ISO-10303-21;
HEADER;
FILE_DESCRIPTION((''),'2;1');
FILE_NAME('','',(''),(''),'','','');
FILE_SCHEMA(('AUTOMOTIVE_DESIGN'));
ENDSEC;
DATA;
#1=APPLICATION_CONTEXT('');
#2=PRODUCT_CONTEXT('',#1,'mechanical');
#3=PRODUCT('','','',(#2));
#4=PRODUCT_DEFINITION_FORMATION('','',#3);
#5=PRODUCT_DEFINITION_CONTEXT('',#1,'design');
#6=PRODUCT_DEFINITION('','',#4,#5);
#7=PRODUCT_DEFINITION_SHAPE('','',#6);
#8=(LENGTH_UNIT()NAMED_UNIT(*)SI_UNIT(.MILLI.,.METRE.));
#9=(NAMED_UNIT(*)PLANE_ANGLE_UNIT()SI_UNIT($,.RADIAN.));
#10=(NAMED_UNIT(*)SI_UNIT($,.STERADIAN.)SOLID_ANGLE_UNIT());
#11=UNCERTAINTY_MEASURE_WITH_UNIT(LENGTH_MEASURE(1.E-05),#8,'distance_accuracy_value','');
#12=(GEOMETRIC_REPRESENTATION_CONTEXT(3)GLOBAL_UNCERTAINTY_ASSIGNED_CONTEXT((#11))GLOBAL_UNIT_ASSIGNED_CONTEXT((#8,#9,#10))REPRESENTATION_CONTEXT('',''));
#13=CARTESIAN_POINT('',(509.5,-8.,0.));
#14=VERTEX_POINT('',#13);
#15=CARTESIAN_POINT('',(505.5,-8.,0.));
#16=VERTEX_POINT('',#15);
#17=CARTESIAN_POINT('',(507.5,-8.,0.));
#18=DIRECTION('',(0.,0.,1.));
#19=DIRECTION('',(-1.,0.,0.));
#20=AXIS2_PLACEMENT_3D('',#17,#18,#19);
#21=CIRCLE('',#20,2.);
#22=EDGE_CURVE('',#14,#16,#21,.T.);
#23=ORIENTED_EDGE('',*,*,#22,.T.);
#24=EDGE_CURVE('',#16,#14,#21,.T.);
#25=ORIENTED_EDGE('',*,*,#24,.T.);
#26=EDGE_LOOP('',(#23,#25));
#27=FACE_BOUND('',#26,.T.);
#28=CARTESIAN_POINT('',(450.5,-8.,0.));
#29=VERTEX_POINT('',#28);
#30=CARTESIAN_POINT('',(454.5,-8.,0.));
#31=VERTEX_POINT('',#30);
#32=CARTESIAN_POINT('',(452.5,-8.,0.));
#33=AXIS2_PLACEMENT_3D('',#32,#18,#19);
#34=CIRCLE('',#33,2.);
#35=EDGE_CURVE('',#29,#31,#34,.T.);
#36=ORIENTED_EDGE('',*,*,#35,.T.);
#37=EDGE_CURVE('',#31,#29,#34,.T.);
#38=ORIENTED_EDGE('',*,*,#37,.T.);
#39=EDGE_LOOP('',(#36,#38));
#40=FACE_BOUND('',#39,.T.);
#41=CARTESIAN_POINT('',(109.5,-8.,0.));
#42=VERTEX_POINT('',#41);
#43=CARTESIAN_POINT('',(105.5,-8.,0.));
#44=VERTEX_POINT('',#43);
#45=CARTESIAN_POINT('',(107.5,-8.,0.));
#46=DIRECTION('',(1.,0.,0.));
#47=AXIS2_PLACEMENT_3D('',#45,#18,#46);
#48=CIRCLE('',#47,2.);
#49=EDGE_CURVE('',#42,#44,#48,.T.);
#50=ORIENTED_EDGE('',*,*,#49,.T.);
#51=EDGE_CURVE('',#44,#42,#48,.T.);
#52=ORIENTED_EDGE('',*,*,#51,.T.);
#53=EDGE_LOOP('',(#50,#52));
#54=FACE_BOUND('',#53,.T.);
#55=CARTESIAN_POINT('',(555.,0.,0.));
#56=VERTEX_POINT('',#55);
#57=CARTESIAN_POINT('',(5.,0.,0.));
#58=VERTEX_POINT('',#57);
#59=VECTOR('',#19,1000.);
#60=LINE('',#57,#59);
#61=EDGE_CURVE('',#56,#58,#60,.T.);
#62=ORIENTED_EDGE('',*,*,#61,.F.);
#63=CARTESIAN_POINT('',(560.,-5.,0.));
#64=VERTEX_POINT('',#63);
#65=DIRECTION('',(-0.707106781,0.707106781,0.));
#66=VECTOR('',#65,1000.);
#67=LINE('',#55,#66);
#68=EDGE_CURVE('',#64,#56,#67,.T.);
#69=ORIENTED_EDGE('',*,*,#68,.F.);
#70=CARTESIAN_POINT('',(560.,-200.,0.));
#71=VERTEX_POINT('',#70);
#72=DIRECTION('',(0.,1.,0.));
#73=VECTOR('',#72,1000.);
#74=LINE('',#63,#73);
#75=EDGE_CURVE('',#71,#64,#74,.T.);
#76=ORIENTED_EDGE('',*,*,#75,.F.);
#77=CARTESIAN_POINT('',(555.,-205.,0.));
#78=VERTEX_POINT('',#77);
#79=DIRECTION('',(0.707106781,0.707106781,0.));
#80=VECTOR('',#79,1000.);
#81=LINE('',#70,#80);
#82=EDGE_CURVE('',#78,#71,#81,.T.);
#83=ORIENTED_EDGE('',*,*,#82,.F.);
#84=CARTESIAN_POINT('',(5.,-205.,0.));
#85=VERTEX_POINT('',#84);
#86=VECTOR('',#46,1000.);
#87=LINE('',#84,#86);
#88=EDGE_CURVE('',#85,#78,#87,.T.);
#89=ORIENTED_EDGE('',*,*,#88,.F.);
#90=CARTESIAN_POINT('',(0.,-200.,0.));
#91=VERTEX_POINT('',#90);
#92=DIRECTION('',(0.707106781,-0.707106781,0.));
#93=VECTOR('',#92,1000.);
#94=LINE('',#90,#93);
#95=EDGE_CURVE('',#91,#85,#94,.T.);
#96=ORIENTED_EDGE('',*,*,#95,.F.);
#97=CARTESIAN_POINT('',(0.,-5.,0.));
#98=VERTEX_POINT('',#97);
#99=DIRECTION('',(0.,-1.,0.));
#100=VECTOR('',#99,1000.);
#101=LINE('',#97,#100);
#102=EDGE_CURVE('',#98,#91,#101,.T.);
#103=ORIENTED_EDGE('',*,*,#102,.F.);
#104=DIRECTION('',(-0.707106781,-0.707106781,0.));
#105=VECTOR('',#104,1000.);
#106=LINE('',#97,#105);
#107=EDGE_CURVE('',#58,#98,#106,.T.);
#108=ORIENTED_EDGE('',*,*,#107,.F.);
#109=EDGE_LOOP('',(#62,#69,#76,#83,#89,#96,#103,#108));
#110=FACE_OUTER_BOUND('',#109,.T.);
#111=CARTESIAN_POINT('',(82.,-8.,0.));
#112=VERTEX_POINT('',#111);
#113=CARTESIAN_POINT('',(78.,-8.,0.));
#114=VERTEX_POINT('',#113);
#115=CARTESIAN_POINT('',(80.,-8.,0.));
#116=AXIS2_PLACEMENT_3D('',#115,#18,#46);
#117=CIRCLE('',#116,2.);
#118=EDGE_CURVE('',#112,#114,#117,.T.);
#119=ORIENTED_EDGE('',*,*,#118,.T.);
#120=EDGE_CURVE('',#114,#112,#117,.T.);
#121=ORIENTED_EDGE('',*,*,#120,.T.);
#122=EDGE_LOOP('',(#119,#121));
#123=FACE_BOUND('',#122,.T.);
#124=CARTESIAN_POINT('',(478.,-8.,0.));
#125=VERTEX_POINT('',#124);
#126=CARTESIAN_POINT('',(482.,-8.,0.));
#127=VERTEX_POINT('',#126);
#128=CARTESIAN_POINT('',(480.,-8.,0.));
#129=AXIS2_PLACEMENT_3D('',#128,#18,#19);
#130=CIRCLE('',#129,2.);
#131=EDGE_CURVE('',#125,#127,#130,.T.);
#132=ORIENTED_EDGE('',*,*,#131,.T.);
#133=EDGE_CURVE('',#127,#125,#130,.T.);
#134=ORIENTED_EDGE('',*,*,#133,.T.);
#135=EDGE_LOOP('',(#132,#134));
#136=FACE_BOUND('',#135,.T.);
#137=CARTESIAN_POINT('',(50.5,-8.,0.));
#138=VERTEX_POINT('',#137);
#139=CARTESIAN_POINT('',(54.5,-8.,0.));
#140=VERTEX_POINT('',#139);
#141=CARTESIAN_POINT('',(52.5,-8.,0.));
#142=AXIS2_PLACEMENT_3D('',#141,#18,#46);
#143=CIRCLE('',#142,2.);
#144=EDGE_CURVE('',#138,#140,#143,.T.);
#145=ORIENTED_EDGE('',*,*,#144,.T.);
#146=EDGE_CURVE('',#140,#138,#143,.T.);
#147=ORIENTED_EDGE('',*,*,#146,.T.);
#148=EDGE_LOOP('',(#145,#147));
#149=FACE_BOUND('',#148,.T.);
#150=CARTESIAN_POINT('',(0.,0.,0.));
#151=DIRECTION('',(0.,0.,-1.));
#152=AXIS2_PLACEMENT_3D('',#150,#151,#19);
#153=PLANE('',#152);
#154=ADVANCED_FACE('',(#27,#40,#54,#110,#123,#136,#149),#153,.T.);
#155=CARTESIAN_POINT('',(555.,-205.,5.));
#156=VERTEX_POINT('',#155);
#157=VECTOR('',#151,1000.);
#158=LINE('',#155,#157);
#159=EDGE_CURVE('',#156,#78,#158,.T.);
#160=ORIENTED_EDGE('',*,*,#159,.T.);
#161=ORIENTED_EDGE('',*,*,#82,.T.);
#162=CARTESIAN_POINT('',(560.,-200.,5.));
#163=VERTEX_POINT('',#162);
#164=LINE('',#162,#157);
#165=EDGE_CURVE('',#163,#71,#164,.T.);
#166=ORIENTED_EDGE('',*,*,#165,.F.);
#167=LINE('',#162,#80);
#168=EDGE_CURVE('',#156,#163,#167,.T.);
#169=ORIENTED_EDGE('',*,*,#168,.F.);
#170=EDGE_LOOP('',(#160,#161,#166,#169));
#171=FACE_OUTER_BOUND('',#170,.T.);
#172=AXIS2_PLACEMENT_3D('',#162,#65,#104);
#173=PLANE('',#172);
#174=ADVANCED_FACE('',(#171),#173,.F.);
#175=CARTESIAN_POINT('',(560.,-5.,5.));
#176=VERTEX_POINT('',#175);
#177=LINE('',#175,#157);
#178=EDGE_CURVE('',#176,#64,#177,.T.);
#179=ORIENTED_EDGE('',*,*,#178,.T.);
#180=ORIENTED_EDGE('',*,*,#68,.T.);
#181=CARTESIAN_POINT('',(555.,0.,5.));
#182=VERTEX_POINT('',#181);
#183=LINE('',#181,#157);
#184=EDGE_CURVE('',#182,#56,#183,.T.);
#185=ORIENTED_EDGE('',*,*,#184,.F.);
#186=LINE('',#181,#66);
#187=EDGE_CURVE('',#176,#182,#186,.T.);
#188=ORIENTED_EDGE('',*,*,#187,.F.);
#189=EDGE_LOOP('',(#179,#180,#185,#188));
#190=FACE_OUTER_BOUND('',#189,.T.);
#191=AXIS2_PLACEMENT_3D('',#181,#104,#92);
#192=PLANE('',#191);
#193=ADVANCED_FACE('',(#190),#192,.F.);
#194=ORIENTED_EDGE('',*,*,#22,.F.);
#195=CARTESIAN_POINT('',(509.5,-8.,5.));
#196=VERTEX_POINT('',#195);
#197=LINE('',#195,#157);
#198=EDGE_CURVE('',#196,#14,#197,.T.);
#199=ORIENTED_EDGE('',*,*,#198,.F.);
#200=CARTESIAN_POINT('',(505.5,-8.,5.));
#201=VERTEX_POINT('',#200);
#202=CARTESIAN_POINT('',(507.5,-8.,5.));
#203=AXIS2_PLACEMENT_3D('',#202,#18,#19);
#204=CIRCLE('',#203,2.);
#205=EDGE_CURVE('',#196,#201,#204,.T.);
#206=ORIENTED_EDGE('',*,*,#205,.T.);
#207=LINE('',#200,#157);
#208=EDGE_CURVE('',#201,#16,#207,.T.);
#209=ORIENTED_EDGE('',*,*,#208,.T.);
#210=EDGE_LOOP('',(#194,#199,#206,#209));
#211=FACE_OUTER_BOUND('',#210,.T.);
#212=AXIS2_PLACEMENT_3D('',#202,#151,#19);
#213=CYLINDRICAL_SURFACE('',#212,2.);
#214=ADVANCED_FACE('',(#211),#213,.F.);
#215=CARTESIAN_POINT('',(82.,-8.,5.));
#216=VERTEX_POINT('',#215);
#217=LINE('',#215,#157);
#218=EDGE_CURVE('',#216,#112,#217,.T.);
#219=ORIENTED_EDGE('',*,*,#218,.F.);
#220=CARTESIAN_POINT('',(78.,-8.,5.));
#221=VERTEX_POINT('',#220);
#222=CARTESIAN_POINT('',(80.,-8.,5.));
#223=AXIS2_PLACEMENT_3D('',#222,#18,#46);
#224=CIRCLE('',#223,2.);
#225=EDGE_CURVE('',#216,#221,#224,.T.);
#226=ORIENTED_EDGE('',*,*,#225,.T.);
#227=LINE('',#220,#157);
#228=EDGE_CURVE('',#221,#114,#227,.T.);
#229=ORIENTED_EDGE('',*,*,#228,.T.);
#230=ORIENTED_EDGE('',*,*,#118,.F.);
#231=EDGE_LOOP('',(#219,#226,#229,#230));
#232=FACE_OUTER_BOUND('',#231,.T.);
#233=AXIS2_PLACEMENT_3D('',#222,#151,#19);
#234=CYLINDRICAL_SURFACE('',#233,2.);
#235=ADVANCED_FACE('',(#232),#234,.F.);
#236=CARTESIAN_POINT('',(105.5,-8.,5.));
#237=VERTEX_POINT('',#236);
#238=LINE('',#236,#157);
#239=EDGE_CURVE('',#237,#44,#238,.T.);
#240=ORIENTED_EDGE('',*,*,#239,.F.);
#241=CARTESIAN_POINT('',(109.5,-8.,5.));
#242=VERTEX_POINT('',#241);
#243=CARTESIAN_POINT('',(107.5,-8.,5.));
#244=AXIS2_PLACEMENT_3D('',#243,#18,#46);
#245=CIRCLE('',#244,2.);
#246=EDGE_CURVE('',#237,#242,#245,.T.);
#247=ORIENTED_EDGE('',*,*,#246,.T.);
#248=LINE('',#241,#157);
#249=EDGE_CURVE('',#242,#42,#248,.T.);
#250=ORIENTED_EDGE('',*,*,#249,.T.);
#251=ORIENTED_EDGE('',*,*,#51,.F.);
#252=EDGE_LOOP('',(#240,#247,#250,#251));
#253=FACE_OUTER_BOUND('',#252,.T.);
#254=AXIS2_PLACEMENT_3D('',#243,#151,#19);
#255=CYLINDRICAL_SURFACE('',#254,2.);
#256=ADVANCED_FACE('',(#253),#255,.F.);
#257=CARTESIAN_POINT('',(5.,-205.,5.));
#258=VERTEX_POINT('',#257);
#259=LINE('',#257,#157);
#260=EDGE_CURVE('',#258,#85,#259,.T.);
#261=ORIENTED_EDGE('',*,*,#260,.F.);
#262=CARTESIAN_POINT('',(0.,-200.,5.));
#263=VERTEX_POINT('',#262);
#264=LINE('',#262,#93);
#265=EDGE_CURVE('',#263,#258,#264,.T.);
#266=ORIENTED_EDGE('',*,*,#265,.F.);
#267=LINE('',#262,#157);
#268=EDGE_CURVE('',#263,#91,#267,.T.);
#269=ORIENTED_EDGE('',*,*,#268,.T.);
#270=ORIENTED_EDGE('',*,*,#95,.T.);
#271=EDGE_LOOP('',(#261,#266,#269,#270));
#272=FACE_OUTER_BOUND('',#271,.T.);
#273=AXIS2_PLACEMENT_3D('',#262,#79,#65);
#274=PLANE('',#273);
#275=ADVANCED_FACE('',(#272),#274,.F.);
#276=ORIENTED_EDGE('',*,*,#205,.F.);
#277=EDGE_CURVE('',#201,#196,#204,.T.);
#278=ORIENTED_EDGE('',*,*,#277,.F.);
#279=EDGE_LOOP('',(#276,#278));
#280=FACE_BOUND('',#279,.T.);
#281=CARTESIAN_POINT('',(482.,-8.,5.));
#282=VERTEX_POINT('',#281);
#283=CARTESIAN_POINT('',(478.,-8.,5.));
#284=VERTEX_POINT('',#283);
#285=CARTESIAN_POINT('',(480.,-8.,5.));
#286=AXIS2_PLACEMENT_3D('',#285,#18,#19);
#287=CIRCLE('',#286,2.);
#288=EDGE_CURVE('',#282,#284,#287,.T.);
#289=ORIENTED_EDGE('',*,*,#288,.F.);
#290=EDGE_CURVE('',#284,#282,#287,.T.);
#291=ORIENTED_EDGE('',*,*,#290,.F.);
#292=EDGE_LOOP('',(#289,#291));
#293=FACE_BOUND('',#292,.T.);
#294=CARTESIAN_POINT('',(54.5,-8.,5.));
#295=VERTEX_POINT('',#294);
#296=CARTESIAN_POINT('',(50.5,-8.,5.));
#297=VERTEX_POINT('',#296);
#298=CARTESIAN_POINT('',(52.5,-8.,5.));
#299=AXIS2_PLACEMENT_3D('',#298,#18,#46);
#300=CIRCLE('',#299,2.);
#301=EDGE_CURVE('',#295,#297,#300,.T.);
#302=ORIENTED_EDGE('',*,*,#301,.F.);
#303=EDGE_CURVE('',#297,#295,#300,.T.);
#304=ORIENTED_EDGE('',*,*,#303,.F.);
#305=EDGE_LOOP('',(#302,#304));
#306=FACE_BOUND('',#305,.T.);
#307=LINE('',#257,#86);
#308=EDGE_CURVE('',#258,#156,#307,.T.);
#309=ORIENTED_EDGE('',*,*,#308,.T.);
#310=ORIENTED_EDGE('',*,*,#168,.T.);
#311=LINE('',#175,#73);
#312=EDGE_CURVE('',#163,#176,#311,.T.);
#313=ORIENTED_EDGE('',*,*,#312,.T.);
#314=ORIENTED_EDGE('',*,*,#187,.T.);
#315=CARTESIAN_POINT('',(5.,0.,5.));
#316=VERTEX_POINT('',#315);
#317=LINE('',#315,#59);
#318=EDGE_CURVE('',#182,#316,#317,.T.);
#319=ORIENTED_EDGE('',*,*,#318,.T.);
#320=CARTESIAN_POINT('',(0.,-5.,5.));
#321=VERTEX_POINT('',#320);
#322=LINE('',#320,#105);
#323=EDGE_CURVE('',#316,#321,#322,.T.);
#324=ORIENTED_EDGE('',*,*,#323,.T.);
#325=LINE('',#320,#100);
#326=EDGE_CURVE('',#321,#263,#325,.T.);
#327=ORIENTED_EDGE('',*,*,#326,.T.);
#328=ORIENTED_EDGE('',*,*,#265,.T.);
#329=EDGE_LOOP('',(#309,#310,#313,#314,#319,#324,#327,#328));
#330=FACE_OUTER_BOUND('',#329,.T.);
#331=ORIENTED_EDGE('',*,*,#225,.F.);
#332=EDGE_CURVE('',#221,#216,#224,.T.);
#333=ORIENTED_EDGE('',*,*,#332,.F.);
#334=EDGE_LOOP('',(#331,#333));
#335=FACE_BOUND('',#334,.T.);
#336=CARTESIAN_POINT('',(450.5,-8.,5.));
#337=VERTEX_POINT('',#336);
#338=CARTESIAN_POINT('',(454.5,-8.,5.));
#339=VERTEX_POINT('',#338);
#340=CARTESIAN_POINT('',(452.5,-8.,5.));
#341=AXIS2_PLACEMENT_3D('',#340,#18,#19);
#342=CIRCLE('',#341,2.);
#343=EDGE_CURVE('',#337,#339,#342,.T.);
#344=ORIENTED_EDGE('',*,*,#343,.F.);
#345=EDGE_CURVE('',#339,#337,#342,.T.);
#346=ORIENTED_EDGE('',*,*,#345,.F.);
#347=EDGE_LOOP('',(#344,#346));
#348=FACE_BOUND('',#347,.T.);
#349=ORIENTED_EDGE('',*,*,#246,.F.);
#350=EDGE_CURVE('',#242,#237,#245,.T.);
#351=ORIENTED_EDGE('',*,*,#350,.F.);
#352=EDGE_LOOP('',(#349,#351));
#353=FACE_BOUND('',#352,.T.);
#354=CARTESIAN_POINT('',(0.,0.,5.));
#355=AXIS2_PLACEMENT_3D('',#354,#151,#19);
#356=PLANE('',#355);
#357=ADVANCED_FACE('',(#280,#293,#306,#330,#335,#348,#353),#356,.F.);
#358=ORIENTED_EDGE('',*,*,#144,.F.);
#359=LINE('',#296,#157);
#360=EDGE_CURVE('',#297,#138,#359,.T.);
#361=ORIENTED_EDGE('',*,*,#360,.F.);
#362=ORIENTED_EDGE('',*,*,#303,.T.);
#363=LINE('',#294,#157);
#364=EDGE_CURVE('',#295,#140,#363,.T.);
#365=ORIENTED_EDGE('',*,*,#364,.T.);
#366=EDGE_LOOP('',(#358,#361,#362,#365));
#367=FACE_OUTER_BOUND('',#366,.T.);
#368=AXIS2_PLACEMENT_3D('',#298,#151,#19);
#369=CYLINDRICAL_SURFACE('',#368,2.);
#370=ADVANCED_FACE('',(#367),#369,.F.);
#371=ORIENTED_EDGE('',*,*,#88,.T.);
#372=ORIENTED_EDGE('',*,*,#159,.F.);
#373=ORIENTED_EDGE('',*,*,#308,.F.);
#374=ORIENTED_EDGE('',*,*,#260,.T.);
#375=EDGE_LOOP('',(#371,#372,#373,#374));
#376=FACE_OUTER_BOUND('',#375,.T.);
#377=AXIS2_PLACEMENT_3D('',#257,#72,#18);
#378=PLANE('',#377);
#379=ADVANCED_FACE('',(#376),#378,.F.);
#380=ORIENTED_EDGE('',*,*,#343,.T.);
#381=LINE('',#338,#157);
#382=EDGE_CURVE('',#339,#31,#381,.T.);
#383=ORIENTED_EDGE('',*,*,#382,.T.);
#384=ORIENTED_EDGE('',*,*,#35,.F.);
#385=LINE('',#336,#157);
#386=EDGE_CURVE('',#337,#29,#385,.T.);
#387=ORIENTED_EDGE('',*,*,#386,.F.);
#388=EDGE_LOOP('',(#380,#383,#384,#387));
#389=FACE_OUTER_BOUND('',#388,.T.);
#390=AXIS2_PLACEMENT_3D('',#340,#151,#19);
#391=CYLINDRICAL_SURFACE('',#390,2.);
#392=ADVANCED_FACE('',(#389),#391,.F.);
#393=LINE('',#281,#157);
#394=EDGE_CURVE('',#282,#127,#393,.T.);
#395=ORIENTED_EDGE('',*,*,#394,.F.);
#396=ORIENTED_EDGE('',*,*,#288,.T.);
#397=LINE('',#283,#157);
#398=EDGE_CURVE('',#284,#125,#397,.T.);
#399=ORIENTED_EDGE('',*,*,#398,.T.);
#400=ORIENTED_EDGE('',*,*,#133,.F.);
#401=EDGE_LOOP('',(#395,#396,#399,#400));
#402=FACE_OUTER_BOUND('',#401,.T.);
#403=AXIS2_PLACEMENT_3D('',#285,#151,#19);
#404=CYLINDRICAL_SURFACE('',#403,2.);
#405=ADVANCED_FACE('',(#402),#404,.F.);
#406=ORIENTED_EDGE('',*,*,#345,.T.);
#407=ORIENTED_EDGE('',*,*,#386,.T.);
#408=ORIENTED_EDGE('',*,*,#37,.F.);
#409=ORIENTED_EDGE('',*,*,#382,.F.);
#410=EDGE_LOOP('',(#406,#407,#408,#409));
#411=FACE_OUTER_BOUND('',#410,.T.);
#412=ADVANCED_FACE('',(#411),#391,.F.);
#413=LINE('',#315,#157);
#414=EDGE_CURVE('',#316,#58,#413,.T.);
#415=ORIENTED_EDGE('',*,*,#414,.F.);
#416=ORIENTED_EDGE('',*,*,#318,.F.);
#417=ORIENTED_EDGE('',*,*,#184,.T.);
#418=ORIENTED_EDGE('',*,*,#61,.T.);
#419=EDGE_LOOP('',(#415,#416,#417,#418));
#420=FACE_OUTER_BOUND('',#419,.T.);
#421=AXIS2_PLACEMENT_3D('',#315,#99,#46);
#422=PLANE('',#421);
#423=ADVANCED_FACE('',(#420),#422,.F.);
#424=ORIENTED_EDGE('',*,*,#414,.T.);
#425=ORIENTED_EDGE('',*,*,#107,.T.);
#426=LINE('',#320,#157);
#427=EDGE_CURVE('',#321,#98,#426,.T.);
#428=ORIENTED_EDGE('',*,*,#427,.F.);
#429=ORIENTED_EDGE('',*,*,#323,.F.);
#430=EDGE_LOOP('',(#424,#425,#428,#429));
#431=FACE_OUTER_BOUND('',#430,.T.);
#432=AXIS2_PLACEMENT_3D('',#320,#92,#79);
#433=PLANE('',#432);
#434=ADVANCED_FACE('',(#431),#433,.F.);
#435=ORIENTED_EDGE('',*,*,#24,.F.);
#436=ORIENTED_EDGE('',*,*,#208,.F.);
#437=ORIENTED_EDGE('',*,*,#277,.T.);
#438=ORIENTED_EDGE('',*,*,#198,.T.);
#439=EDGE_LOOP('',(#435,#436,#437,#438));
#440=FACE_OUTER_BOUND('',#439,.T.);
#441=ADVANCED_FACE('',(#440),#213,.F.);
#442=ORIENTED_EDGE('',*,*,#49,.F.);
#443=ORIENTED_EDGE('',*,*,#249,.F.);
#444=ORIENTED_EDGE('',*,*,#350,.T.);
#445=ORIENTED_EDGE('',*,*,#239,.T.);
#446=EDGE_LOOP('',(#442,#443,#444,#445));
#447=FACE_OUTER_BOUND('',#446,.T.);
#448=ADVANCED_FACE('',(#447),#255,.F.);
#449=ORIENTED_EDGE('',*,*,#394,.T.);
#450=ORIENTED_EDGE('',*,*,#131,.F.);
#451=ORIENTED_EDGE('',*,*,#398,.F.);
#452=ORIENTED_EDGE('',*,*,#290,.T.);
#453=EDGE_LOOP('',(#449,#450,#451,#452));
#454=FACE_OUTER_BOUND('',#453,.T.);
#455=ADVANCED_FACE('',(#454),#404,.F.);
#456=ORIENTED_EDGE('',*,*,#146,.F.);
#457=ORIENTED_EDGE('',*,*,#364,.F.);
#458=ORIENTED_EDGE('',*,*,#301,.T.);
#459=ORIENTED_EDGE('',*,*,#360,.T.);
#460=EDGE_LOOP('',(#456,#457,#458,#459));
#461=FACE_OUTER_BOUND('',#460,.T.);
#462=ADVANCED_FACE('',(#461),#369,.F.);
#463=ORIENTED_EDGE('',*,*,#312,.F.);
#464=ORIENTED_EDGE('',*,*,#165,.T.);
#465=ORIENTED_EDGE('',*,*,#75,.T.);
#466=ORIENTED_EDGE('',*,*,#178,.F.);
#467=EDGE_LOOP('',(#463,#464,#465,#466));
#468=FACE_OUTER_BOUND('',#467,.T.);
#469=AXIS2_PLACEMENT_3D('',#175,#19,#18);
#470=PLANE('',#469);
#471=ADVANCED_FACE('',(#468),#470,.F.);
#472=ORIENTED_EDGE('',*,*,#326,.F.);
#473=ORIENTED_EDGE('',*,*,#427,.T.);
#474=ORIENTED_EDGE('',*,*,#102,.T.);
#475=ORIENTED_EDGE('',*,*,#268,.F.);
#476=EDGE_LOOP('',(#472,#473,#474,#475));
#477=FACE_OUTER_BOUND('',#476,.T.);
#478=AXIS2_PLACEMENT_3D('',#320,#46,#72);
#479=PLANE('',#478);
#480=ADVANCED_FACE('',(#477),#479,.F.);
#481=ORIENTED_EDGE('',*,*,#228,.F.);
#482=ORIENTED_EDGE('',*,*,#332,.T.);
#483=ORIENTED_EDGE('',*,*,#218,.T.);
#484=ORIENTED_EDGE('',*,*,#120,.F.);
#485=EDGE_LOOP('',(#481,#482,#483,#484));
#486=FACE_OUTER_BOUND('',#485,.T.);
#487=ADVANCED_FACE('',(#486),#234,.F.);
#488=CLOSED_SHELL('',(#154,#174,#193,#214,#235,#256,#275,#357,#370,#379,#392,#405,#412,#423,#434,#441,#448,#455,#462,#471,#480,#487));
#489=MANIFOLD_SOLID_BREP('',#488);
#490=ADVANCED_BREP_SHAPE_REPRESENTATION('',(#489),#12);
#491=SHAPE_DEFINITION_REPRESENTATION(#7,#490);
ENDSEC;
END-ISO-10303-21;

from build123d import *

# Parameters (mm, degrees)
SKETCH1_R           = 2
BOSS_EXTRUDE1_DEPTH = 5


with BuildPart() as part:
    # Sketch1 → Boss-Extrude1 (new body)
    with BuildSketch(Plane.XY):
        Polygon((0, -5), (5, 0), (555, 0), (560, -5), (560, -200), (555, -205), (5, -205), (0, -200), align=None)
        with Locations((52.5, -8)):
            Circle(SKETCH1_R, mode=Mode.SUBTRACT)
        with Locations((80, -8)):
            Circle(SKETCH1_R, mode=Mode.SUBTRACT)
        with Locations((107.5, -8)):
            Circle(SKETCH1_R, mode=Mode.SUBTRACT)
        with Locations(Location((452.5, -8, 0), (0, 0, 180))):
            Circle(SKETCH1_R, mode=Mode.SUBTRACT)
        with Locations(Location((480, -8, 0), (0, 0, 180))):
            Circle(SKETCH1_R, mode=Mode.SUBTRACT)
        with Locations(Location((507.5, -8, 0), (0, 0, 180))):
            Circle(SKETCH1_R, mode=Mode.SUBTRACT)
    extrude(amount=BOSS_EXTRUDE1_DEPTH)


solid = part.part
